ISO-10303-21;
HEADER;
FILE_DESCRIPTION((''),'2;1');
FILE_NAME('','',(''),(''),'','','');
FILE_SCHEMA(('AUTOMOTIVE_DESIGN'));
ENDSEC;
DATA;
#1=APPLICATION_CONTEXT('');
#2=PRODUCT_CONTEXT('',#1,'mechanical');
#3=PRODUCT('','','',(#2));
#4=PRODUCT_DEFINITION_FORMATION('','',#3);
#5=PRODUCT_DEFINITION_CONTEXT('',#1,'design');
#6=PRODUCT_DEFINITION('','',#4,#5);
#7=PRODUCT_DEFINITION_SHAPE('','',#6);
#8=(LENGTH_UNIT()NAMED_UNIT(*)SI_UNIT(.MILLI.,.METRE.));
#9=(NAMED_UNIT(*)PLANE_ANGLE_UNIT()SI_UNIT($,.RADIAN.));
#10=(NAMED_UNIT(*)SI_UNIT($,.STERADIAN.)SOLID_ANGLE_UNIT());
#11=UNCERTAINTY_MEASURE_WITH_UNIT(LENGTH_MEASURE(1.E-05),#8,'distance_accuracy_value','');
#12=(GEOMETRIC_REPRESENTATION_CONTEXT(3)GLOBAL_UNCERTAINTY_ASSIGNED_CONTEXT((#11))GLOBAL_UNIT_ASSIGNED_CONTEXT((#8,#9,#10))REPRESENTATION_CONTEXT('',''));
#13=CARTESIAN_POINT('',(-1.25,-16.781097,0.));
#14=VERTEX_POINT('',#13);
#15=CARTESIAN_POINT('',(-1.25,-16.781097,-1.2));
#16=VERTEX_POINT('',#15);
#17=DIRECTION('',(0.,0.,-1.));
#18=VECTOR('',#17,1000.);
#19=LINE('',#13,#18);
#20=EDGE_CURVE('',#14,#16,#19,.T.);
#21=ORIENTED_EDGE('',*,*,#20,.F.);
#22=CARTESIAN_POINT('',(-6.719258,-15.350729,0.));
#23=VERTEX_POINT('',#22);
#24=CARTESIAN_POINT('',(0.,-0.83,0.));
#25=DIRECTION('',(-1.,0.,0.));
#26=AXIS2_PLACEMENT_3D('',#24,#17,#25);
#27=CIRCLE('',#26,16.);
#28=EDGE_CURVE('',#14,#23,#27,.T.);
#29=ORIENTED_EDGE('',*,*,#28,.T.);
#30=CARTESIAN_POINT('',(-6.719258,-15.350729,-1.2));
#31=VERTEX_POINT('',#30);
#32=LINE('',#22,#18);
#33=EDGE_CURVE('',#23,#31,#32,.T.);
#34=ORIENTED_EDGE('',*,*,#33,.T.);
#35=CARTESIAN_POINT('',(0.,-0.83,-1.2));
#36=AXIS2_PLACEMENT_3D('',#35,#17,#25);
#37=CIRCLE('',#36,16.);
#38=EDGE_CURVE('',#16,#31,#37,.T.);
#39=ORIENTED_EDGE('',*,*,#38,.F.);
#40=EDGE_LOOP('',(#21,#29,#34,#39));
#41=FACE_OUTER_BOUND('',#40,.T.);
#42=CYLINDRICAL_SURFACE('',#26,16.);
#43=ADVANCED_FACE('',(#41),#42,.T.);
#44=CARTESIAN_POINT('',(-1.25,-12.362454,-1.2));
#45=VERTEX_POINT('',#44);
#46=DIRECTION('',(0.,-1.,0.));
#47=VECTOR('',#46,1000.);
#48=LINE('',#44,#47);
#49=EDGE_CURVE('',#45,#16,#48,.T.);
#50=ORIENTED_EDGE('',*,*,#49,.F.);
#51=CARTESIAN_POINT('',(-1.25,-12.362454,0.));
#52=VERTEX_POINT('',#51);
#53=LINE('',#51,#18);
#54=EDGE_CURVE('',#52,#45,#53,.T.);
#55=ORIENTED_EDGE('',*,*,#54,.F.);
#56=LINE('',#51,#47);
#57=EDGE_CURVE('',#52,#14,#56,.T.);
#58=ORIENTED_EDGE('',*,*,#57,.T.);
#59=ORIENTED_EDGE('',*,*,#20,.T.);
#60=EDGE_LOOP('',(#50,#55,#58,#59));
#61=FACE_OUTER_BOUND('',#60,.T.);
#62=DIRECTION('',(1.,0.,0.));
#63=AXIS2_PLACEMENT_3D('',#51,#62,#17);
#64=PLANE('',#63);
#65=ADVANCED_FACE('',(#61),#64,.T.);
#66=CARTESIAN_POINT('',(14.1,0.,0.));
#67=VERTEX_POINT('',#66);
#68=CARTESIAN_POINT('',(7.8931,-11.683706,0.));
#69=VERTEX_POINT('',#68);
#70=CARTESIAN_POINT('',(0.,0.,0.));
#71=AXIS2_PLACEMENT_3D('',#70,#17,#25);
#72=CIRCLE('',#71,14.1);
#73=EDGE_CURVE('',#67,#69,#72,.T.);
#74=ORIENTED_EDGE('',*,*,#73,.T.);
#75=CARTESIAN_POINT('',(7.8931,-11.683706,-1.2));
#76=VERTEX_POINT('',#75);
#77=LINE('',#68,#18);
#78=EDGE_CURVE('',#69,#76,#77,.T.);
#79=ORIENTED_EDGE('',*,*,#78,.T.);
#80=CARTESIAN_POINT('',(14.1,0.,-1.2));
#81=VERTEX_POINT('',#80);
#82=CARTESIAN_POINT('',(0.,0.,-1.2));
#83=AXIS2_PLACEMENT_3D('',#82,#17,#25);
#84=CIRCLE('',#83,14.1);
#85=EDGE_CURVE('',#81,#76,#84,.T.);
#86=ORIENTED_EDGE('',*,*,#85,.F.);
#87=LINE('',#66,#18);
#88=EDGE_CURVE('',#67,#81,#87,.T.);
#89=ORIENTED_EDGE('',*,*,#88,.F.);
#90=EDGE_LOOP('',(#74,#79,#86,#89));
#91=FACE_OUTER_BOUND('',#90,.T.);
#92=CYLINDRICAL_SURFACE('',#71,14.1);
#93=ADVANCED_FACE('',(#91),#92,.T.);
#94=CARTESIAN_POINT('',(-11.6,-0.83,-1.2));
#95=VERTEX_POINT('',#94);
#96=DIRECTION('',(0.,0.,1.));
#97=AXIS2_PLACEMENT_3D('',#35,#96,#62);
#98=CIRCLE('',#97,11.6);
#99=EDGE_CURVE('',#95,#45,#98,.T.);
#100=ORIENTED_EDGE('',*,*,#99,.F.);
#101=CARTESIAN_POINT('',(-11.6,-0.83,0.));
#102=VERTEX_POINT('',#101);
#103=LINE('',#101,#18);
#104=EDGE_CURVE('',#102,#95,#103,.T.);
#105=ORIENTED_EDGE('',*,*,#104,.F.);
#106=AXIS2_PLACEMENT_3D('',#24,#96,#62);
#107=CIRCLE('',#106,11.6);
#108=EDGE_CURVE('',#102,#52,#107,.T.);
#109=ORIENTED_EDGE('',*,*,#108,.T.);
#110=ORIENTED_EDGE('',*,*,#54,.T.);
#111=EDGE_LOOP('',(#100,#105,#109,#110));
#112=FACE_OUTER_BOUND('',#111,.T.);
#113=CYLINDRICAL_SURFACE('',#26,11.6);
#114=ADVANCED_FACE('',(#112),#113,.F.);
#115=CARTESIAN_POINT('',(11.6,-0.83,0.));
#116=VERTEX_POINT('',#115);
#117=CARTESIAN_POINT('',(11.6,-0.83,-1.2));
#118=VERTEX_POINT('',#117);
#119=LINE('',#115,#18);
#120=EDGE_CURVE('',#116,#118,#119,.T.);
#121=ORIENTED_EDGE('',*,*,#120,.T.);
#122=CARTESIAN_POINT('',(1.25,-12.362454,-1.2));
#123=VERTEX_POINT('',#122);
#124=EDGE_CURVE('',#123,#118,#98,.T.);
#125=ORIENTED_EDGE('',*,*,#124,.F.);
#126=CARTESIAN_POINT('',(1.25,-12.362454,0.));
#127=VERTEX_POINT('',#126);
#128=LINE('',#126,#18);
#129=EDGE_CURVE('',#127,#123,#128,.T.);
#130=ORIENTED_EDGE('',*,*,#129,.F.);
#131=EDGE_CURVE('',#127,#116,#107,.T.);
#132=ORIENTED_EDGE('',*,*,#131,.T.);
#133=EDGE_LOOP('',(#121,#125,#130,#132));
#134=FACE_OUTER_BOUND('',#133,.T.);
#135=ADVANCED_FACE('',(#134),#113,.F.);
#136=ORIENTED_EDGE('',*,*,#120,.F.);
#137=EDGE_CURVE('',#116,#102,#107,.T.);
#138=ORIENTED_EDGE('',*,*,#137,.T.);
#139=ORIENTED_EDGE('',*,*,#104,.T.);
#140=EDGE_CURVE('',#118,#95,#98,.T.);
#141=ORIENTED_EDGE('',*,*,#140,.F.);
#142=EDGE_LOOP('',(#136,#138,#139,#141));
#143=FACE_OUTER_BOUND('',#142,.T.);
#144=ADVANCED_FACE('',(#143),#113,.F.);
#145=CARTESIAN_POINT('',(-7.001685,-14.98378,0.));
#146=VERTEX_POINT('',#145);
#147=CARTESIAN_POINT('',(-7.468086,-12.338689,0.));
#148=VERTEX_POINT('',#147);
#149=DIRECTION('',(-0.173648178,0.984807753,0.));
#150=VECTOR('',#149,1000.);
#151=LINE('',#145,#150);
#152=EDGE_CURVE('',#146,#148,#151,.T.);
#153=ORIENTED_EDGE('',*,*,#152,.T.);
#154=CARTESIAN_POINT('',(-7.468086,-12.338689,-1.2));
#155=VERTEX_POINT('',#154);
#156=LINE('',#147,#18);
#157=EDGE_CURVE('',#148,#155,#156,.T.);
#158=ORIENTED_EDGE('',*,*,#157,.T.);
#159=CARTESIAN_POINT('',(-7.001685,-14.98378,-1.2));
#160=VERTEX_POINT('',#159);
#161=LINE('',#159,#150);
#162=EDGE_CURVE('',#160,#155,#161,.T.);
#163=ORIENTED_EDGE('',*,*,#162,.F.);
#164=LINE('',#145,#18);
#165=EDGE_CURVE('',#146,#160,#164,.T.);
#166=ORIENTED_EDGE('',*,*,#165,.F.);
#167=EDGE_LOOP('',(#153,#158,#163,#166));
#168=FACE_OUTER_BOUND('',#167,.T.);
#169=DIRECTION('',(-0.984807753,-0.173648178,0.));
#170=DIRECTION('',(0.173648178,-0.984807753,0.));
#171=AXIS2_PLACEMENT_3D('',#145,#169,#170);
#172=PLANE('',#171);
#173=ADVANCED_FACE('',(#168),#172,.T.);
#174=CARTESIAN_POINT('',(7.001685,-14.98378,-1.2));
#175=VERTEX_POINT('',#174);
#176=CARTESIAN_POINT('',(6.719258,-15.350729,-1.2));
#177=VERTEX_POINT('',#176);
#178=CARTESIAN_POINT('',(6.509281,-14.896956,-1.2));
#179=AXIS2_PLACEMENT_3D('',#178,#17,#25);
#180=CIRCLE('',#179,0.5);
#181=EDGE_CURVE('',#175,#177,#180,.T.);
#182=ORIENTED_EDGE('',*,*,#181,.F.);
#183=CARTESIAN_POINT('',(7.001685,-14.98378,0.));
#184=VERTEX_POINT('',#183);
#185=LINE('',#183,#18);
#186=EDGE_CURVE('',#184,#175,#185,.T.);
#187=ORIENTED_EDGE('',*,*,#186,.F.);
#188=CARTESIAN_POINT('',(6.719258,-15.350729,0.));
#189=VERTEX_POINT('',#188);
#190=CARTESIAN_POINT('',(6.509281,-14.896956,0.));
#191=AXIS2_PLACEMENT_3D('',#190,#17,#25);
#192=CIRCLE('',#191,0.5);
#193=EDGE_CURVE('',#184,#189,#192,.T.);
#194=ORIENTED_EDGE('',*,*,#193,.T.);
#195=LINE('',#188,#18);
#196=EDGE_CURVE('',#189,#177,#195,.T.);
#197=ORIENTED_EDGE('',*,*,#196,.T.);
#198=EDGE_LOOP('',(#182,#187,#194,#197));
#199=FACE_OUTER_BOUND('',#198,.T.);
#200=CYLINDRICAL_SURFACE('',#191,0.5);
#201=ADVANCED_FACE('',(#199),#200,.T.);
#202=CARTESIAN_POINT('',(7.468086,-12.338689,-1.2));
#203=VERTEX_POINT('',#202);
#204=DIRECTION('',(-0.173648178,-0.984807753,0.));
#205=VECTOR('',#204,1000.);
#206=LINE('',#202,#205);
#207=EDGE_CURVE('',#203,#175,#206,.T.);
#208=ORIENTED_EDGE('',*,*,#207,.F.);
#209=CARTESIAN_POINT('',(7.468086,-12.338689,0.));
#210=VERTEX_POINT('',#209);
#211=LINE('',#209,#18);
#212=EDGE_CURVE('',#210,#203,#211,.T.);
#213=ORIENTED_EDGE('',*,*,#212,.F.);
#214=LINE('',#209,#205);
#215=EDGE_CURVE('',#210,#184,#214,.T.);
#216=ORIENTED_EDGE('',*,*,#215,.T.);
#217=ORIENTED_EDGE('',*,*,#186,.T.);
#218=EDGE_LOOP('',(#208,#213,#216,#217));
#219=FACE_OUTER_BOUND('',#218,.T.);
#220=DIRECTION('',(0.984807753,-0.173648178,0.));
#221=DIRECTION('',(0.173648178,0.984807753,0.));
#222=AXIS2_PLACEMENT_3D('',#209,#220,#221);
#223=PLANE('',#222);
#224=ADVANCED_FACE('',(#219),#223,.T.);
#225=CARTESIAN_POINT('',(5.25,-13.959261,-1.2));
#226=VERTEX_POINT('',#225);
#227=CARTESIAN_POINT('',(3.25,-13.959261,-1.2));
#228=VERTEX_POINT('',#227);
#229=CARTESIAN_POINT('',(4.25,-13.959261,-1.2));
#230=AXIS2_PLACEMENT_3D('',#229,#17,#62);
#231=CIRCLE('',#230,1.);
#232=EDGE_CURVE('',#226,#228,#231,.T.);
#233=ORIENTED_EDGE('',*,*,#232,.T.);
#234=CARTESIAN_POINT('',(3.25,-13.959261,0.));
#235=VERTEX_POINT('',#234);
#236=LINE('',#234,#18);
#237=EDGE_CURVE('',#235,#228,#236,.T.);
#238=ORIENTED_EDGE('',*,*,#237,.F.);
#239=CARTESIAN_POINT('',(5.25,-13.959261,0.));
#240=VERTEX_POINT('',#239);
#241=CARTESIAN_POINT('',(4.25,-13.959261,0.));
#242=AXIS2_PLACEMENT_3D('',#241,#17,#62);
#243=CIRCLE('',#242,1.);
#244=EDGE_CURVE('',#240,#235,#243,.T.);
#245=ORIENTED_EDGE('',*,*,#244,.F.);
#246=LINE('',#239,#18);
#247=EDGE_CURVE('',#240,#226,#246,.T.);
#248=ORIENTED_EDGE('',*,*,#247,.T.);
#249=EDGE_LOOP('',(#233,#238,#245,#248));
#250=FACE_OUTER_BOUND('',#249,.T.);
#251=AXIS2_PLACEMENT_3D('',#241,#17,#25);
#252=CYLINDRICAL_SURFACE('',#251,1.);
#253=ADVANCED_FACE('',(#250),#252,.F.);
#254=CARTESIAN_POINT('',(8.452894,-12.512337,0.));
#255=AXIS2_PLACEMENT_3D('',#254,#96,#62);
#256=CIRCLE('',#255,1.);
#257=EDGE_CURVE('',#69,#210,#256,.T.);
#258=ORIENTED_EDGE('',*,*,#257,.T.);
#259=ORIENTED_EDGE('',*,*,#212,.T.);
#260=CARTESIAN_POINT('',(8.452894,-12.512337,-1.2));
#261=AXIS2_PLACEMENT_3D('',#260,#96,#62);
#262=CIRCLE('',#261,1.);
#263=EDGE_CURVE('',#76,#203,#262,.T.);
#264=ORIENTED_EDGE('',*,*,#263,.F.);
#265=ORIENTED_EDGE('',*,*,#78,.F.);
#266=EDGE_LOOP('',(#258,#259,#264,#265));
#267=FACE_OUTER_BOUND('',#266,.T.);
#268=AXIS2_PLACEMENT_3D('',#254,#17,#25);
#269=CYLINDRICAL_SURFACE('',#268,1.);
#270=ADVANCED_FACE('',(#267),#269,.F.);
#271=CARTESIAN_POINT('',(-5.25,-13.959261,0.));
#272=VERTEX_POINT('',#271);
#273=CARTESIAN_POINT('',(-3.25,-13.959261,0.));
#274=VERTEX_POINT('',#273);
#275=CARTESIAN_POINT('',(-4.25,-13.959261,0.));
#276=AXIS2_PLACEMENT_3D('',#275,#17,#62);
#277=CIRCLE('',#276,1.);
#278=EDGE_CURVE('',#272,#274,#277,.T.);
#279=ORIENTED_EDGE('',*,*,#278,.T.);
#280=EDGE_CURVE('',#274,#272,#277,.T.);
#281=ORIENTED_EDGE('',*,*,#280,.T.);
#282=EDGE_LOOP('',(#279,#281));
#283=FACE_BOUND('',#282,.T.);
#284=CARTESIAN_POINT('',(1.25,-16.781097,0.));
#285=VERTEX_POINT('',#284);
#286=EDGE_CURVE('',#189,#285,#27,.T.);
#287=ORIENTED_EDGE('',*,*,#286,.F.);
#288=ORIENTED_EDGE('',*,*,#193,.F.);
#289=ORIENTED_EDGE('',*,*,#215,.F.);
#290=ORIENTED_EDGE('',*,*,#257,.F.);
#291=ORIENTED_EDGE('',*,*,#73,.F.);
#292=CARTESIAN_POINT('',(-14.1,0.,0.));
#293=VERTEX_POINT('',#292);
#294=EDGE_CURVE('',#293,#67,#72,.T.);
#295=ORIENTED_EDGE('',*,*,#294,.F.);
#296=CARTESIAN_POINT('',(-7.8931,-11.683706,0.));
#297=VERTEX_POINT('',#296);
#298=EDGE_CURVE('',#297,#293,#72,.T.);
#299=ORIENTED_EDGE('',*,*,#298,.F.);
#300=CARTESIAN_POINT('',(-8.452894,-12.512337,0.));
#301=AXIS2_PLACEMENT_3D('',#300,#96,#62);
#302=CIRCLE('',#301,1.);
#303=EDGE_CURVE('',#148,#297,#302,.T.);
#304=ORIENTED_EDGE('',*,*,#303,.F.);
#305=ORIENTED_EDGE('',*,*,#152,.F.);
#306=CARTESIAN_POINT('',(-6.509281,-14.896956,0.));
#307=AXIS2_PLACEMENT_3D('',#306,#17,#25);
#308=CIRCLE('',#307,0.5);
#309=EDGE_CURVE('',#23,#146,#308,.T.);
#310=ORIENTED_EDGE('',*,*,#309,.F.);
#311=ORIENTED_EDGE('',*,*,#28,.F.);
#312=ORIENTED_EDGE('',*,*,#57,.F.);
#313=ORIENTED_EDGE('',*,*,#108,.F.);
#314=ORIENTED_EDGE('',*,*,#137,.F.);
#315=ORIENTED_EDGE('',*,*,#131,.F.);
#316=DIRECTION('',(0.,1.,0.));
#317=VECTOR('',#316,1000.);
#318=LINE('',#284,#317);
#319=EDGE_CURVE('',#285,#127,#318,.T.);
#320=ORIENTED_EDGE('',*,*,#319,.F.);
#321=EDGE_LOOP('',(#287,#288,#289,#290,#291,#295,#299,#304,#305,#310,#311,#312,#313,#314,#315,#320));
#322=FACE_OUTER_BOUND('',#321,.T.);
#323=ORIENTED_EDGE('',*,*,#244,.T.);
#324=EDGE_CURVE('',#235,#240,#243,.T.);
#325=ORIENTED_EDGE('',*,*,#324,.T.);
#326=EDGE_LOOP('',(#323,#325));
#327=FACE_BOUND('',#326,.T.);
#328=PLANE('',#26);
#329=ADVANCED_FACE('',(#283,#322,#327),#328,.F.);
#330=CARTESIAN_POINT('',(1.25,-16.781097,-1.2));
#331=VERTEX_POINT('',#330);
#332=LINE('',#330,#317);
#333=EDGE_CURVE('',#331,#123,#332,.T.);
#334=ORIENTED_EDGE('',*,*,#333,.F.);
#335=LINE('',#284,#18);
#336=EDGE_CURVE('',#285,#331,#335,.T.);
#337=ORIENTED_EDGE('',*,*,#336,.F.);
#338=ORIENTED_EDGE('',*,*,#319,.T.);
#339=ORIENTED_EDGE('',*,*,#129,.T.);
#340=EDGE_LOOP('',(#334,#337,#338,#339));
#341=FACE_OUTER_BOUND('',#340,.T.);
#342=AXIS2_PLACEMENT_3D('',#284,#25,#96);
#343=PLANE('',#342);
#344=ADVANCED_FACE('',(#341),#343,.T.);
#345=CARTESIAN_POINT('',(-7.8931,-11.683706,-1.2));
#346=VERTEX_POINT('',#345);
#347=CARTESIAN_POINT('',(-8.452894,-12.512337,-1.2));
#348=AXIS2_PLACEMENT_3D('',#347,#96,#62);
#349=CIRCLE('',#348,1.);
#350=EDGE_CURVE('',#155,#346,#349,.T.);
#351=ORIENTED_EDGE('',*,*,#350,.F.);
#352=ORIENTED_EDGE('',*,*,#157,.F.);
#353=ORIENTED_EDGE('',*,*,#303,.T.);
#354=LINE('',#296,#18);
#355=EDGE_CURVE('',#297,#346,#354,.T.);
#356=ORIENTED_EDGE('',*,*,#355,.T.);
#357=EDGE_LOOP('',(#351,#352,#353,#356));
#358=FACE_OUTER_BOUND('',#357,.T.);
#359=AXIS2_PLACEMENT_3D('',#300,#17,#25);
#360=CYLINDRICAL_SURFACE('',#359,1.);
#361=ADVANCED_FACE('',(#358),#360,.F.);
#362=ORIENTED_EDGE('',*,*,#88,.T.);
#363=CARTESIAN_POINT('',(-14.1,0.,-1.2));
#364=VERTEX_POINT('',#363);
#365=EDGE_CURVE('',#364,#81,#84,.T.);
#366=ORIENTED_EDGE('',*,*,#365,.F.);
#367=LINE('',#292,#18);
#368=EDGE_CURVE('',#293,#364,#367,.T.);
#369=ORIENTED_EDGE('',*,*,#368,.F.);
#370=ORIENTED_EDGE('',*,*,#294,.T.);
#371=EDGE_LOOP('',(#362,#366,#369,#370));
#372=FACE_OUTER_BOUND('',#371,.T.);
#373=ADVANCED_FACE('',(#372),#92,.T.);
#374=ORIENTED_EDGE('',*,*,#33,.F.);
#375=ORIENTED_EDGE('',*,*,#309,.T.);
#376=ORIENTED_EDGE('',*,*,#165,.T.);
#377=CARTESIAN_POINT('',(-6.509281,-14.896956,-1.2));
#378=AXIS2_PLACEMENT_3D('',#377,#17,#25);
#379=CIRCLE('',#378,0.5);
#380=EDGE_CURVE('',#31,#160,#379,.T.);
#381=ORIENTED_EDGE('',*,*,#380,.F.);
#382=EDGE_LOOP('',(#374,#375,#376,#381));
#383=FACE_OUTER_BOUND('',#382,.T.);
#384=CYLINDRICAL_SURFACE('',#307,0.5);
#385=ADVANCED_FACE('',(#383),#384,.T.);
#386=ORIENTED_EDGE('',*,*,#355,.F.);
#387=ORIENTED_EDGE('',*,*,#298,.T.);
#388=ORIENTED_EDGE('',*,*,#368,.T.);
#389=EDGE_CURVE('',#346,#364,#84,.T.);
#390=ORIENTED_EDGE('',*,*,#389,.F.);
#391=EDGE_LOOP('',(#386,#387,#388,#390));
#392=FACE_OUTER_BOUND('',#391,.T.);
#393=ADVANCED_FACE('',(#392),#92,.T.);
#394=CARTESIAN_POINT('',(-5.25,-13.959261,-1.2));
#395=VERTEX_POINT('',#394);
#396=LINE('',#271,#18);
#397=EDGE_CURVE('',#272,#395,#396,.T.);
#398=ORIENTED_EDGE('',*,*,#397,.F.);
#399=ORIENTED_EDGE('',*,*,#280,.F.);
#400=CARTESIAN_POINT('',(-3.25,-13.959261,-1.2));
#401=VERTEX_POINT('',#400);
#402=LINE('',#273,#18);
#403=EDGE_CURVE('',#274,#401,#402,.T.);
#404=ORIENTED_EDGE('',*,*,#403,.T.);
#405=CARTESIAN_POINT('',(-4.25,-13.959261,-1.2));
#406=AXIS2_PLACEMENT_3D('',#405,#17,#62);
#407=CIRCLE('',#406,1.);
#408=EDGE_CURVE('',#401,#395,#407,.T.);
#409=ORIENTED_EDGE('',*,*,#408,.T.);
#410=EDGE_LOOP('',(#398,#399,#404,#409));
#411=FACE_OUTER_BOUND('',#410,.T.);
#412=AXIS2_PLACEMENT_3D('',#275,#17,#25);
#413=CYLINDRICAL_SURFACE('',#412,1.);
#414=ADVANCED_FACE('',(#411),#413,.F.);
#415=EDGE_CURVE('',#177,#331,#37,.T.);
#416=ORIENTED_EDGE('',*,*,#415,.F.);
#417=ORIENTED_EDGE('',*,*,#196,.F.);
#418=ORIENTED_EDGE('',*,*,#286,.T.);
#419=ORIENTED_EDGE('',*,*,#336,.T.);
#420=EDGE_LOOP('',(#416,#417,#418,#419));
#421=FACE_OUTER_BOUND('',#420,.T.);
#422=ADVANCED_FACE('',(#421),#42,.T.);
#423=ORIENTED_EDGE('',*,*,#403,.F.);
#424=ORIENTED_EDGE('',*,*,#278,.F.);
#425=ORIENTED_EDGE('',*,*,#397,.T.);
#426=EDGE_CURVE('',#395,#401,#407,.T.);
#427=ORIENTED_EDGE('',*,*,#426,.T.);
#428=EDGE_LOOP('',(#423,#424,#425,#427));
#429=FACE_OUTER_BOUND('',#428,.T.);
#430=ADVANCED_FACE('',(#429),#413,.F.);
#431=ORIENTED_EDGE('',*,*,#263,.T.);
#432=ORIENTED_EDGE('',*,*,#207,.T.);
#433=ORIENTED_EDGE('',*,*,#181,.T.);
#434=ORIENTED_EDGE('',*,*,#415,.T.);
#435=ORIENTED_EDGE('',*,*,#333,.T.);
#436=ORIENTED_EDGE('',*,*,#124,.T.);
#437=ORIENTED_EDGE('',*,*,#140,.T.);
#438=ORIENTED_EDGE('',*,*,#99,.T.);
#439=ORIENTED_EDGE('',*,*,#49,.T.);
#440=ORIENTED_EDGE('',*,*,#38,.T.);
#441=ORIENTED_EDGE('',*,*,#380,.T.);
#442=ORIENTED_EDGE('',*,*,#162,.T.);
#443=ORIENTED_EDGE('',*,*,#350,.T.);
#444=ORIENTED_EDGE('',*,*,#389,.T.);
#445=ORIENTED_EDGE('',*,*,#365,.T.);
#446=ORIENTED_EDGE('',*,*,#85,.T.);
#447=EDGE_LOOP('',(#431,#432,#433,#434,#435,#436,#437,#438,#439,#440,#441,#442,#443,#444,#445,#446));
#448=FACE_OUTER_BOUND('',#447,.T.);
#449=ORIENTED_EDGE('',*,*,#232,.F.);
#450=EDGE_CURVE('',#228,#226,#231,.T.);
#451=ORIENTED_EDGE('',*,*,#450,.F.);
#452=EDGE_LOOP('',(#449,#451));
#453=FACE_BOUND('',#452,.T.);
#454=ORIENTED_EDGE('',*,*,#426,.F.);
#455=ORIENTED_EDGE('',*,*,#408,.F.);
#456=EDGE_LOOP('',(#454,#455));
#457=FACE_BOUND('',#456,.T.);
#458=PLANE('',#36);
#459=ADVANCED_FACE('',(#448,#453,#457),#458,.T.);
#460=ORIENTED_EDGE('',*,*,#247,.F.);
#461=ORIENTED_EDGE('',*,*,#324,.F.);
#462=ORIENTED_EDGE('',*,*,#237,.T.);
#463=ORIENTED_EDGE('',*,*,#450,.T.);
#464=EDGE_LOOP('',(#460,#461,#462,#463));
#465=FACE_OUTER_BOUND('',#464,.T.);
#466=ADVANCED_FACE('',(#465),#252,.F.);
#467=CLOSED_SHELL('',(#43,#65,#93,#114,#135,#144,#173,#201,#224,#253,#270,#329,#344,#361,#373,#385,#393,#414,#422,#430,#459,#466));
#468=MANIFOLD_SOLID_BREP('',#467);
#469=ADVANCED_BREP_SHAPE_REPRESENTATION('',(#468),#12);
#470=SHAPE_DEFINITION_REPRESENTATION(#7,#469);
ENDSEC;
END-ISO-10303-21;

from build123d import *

# Parameters (mm, degrees)
SKETCH_1_R      = 1
EXTRUDE_1_DEPTH = 1.2


with BuildPart() as part:
    # 草图1 → 凸台-拉伸1 (new body)
    with BuildSketch(Plane(origin=(0, 0, -1.2), x_dir=(-1, 0, 0), z_dir=(0, 0, -1))):
        with BuildLine():
            Line((-1.25, -16.781097141), (-1.25, -12.362454205))
            ThreePointArc((-1.25, -12.362454205), (0, 10.77), (1.25, -12.362454205))
            Line((1.25, -12.362454205), (1.25, -16.781097141))
            ThreePointArc((1.25, -16.781097141), (4.048302979, -16.309381221), (6.719258119, -15.350728987))
            ThreePointArc((6.719258119, -15.350728987), (6.905510397, -15.201919327), (7.00168518, -14.983780295))
            Line((7.00168518, -14.983780295), (7.468086116, -12.338689143))
            ThreePointArc((7.468086116, -12.338689143), (7.614025765, -11.968002587), (7.893099573, -11.68370571))
            ThreePointArc((7.893099573, -11.68370571), (0, 14.1), (-7.893099573, -11.68370571))
            ThreePointArc((-7.893099573, -11.68370571), (-7.614025765, -11.968002587), (-7.468086116, -12.338689143))
            Line((-7.468086116, -12.338689143), (-7.00168518, -14.983780295))
            ThreePointArc((-7.00168518, -14.983780295), (-6.905510397, -15.201919327), (-6.719258119, -15.350728987))
            ThreePointArc((-6.719258119, -15.350728987), (-4.048302979, -16.309381221), (-1.25, -16.781097141))
        make_face()
        with Locations(Location((-4.25, -13.959261213, 0), (0, 0, 180))):
            Circle(SKETCH_1_R, mode=Mode.SUBTRACT)
        with Locations(Location((4.25, -13.959261213, 0), (0, 0, 180))):
            Circle(SKETCH_1_R, mode=Mode.SUBTRACT)
    extrude(amount=-EXTRUDE_1_DEPTH)


solid = part.part
